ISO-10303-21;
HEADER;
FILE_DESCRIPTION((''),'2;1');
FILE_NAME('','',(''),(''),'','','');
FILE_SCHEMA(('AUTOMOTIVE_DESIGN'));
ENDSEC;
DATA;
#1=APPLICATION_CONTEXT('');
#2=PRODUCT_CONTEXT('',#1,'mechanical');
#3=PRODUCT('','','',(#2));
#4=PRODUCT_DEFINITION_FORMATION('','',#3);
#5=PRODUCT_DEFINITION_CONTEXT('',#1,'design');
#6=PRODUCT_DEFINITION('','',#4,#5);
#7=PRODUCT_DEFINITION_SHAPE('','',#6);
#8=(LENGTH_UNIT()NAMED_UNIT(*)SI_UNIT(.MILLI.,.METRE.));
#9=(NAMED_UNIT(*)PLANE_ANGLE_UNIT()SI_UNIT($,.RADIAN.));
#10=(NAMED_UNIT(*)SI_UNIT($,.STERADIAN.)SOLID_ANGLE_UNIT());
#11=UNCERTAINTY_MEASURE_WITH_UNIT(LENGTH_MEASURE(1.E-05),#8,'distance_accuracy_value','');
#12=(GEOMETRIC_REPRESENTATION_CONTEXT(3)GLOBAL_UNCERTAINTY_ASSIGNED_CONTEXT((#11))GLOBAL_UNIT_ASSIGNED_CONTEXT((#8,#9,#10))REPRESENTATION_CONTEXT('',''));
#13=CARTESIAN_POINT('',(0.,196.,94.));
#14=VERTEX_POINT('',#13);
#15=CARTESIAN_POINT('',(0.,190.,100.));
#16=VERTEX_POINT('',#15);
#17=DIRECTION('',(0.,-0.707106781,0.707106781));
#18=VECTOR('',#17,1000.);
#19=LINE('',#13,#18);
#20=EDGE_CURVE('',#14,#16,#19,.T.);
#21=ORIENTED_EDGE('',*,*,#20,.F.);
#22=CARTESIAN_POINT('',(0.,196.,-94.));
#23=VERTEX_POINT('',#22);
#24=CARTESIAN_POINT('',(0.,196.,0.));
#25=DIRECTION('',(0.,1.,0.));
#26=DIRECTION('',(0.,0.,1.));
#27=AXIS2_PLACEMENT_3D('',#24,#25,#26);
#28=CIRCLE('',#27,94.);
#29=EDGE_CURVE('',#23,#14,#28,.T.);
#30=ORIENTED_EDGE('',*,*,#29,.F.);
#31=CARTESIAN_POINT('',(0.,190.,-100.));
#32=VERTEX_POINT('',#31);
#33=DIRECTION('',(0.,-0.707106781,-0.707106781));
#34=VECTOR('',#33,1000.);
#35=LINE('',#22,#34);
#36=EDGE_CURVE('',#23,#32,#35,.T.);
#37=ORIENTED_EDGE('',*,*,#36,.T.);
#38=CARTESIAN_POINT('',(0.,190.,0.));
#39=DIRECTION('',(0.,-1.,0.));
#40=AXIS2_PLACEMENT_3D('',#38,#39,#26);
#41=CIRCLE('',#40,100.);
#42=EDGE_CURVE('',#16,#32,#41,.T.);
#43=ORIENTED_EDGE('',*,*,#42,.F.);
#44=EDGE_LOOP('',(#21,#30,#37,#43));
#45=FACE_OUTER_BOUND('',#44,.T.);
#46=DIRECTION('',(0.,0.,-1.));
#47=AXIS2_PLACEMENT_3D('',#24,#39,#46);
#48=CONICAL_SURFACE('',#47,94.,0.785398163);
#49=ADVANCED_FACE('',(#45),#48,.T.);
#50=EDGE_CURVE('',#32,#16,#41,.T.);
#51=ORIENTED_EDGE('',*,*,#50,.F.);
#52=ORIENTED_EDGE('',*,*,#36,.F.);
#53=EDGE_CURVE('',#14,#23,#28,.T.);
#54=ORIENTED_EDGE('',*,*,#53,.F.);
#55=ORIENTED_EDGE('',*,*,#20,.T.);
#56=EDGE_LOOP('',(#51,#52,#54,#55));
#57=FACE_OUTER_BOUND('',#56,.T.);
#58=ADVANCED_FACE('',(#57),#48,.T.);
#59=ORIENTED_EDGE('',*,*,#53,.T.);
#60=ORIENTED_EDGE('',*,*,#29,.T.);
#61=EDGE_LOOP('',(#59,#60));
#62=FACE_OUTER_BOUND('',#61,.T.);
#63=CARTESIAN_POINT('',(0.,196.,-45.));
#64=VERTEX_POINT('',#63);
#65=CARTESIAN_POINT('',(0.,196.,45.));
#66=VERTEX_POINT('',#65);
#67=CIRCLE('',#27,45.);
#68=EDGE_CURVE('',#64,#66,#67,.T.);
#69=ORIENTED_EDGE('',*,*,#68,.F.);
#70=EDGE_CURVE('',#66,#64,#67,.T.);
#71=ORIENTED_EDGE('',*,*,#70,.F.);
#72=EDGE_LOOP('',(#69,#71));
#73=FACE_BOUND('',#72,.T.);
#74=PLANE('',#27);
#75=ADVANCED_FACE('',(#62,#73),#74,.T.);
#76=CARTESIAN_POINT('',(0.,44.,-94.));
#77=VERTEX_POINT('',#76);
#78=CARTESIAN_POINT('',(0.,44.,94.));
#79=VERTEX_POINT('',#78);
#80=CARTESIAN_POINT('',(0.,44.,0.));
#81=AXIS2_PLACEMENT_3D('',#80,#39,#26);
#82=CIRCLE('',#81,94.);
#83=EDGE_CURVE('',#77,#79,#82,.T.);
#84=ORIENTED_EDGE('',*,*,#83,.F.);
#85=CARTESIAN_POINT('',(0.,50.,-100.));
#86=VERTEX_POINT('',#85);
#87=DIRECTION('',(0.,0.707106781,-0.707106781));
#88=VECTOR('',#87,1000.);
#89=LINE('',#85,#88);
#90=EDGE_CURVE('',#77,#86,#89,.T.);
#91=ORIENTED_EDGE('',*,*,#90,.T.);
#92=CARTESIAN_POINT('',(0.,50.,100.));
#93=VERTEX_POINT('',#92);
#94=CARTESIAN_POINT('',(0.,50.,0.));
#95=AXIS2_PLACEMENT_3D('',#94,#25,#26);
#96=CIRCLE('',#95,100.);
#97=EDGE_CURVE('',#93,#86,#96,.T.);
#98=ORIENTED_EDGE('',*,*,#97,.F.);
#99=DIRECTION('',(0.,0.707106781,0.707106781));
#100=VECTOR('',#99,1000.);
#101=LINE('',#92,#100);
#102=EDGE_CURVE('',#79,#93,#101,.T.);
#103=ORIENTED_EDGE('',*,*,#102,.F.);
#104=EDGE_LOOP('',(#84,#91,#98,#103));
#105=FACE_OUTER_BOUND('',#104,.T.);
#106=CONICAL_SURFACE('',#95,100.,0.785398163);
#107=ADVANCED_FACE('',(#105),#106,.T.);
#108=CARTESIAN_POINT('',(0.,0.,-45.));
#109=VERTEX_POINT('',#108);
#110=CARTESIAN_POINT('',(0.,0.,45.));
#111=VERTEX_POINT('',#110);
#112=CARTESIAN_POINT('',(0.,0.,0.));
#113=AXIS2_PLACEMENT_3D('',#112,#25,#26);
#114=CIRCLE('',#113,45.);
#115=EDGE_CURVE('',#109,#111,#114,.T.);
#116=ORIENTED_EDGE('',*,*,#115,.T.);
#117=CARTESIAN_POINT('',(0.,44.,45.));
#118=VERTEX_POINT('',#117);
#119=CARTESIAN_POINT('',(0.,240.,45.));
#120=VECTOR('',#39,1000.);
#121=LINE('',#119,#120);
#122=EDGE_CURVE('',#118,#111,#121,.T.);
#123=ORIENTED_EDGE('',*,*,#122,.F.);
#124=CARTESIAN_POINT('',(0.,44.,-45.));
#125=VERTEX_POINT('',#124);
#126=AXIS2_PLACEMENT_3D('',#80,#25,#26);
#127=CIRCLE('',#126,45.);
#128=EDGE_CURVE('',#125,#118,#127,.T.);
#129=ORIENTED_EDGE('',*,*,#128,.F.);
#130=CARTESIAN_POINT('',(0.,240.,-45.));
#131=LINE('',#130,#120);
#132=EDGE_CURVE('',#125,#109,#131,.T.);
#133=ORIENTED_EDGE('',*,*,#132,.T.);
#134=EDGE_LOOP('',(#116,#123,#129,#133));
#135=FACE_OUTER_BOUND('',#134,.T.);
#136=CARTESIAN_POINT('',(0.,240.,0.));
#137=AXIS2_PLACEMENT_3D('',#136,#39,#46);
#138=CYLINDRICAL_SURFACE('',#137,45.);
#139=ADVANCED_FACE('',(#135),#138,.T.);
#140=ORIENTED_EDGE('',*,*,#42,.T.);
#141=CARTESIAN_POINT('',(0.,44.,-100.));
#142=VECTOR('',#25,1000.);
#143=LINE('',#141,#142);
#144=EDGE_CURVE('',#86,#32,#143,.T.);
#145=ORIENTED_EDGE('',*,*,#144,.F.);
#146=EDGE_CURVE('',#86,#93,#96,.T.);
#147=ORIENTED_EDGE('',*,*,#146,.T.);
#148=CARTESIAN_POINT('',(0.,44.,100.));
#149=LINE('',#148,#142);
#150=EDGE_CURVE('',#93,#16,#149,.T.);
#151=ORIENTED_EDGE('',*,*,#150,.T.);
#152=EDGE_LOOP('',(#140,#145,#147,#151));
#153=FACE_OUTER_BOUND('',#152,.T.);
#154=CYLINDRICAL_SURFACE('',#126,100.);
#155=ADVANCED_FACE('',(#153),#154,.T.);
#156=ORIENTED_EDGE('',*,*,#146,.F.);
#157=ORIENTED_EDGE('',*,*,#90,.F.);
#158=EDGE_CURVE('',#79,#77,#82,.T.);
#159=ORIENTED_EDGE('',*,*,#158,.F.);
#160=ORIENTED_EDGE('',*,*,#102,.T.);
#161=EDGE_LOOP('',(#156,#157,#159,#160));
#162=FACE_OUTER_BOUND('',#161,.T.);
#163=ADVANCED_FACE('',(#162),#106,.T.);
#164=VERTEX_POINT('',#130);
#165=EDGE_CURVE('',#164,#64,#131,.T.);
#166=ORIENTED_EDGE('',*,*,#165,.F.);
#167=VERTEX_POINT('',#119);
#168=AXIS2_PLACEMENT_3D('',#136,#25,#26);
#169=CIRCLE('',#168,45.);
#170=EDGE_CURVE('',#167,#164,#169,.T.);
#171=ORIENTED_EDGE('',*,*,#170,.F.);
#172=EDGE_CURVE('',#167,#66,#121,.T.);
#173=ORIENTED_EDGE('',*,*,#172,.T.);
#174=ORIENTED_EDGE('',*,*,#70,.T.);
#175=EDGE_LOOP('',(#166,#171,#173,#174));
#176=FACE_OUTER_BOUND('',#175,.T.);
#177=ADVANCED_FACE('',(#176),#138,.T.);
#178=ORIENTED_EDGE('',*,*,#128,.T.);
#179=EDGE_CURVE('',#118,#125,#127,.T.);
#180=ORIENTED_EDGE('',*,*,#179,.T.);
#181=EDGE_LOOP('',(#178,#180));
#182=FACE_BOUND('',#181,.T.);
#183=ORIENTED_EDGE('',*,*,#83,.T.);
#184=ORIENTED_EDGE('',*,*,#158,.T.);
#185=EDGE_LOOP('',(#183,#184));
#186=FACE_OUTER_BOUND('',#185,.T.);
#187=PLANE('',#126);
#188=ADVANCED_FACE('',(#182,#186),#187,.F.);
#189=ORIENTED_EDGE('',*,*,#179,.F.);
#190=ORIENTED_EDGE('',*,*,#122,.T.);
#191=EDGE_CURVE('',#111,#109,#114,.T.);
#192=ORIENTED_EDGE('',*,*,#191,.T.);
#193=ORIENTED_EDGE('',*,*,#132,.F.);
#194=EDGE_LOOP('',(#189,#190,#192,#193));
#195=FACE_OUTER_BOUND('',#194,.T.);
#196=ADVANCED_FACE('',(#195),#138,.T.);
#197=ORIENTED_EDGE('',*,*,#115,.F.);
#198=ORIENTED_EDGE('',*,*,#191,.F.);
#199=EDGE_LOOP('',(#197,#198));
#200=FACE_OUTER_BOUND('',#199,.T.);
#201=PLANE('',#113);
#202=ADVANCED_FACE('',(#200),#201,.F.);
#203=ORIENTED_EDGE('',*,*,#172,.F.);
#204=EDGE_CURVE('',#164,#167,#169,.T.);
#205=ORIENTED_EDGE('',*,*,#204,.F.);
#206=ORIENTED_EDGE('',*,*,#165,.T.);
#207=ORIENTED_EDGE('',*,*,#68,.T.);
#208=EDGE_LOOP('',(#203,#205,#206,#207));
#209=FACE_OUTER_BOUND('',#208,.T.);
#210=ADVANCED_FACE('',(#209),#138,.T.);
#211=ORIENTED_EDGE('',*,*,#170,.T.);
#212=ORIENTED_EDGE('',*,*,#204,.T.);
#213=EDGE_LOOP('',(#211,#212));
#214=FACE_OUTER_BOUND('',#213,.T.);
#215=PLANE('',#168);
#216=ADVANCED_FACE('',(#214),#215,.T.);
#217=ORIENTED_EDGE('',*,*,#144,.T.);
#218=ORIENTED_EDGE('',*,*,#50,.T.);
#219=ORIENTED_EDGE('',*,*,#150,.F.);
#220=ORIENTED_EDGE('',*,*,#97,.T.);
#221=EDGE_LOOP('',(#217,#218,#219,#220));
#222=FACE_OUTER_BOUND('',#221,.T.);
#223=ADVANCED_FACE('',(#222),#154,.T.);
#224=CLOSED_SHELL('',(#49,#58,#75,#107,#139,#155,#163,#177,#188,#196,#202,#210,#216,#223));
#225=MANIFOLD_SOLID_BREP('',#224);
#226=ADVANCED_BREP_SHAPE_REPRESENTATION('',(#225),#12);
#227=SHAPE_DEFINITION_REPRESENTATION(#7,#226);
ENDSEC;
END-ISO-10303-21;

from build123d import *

# Parameters (mm, degrees)
SKETCH1_R                = 45
BOSS_EXTRUDE1_DEPTH      = 240
BOSS_EXTRUDE2_DEPTH      = 76
BOSS_EXTRUDE2_DEPTH_BACK = 76
SKETCH2_R                = 100
CHAMFER1_SIZE            = 6


with BuildPart() as part:
    # Sketch1 → Boss-Extrude1 (new body)
    with BuildSketch(Plane(origin=(0, 0, 0), x_dir=(1, 0, 0), z_dir=(0, 1, 0))):
        with Locations(Location((0, 0, 0), (0, 0, 270))):
            Circle(SKETCH1_R)
    extrude(amount=BOSS_EXTRUDE1_DEPTH)

    # Sketch2 → Boss-Extrude2 (add, two sides: drawn at the far end of the back side and taken through both)
    with BuildSketch(Plane(origin=(0, 120, 0), x_dir=(1, 0, 0), z_dir=(0, 1, 0)).offset(-BOSS_EXTRUDE2_DEPTH_BACK)):
        with Locations(Location((0, 0, 0), (0, 0, 270))):
            Circle(SKETCH2_R)
    extrude(amount=BOSS_EXTRUDE2_DEPTH + BOSS_EXTRUDE2_DEPTH_BACK)

    # Chamfer1
    chamfer1_edges = [part.edges().sort_by_distance(p)[0] for p in [
        (0, 44, -100),
        (0, 196, -100),
    ]]
    chamfer(chamfer1_edges, length=CHAMFER1_SIZE)


solid = part.part
